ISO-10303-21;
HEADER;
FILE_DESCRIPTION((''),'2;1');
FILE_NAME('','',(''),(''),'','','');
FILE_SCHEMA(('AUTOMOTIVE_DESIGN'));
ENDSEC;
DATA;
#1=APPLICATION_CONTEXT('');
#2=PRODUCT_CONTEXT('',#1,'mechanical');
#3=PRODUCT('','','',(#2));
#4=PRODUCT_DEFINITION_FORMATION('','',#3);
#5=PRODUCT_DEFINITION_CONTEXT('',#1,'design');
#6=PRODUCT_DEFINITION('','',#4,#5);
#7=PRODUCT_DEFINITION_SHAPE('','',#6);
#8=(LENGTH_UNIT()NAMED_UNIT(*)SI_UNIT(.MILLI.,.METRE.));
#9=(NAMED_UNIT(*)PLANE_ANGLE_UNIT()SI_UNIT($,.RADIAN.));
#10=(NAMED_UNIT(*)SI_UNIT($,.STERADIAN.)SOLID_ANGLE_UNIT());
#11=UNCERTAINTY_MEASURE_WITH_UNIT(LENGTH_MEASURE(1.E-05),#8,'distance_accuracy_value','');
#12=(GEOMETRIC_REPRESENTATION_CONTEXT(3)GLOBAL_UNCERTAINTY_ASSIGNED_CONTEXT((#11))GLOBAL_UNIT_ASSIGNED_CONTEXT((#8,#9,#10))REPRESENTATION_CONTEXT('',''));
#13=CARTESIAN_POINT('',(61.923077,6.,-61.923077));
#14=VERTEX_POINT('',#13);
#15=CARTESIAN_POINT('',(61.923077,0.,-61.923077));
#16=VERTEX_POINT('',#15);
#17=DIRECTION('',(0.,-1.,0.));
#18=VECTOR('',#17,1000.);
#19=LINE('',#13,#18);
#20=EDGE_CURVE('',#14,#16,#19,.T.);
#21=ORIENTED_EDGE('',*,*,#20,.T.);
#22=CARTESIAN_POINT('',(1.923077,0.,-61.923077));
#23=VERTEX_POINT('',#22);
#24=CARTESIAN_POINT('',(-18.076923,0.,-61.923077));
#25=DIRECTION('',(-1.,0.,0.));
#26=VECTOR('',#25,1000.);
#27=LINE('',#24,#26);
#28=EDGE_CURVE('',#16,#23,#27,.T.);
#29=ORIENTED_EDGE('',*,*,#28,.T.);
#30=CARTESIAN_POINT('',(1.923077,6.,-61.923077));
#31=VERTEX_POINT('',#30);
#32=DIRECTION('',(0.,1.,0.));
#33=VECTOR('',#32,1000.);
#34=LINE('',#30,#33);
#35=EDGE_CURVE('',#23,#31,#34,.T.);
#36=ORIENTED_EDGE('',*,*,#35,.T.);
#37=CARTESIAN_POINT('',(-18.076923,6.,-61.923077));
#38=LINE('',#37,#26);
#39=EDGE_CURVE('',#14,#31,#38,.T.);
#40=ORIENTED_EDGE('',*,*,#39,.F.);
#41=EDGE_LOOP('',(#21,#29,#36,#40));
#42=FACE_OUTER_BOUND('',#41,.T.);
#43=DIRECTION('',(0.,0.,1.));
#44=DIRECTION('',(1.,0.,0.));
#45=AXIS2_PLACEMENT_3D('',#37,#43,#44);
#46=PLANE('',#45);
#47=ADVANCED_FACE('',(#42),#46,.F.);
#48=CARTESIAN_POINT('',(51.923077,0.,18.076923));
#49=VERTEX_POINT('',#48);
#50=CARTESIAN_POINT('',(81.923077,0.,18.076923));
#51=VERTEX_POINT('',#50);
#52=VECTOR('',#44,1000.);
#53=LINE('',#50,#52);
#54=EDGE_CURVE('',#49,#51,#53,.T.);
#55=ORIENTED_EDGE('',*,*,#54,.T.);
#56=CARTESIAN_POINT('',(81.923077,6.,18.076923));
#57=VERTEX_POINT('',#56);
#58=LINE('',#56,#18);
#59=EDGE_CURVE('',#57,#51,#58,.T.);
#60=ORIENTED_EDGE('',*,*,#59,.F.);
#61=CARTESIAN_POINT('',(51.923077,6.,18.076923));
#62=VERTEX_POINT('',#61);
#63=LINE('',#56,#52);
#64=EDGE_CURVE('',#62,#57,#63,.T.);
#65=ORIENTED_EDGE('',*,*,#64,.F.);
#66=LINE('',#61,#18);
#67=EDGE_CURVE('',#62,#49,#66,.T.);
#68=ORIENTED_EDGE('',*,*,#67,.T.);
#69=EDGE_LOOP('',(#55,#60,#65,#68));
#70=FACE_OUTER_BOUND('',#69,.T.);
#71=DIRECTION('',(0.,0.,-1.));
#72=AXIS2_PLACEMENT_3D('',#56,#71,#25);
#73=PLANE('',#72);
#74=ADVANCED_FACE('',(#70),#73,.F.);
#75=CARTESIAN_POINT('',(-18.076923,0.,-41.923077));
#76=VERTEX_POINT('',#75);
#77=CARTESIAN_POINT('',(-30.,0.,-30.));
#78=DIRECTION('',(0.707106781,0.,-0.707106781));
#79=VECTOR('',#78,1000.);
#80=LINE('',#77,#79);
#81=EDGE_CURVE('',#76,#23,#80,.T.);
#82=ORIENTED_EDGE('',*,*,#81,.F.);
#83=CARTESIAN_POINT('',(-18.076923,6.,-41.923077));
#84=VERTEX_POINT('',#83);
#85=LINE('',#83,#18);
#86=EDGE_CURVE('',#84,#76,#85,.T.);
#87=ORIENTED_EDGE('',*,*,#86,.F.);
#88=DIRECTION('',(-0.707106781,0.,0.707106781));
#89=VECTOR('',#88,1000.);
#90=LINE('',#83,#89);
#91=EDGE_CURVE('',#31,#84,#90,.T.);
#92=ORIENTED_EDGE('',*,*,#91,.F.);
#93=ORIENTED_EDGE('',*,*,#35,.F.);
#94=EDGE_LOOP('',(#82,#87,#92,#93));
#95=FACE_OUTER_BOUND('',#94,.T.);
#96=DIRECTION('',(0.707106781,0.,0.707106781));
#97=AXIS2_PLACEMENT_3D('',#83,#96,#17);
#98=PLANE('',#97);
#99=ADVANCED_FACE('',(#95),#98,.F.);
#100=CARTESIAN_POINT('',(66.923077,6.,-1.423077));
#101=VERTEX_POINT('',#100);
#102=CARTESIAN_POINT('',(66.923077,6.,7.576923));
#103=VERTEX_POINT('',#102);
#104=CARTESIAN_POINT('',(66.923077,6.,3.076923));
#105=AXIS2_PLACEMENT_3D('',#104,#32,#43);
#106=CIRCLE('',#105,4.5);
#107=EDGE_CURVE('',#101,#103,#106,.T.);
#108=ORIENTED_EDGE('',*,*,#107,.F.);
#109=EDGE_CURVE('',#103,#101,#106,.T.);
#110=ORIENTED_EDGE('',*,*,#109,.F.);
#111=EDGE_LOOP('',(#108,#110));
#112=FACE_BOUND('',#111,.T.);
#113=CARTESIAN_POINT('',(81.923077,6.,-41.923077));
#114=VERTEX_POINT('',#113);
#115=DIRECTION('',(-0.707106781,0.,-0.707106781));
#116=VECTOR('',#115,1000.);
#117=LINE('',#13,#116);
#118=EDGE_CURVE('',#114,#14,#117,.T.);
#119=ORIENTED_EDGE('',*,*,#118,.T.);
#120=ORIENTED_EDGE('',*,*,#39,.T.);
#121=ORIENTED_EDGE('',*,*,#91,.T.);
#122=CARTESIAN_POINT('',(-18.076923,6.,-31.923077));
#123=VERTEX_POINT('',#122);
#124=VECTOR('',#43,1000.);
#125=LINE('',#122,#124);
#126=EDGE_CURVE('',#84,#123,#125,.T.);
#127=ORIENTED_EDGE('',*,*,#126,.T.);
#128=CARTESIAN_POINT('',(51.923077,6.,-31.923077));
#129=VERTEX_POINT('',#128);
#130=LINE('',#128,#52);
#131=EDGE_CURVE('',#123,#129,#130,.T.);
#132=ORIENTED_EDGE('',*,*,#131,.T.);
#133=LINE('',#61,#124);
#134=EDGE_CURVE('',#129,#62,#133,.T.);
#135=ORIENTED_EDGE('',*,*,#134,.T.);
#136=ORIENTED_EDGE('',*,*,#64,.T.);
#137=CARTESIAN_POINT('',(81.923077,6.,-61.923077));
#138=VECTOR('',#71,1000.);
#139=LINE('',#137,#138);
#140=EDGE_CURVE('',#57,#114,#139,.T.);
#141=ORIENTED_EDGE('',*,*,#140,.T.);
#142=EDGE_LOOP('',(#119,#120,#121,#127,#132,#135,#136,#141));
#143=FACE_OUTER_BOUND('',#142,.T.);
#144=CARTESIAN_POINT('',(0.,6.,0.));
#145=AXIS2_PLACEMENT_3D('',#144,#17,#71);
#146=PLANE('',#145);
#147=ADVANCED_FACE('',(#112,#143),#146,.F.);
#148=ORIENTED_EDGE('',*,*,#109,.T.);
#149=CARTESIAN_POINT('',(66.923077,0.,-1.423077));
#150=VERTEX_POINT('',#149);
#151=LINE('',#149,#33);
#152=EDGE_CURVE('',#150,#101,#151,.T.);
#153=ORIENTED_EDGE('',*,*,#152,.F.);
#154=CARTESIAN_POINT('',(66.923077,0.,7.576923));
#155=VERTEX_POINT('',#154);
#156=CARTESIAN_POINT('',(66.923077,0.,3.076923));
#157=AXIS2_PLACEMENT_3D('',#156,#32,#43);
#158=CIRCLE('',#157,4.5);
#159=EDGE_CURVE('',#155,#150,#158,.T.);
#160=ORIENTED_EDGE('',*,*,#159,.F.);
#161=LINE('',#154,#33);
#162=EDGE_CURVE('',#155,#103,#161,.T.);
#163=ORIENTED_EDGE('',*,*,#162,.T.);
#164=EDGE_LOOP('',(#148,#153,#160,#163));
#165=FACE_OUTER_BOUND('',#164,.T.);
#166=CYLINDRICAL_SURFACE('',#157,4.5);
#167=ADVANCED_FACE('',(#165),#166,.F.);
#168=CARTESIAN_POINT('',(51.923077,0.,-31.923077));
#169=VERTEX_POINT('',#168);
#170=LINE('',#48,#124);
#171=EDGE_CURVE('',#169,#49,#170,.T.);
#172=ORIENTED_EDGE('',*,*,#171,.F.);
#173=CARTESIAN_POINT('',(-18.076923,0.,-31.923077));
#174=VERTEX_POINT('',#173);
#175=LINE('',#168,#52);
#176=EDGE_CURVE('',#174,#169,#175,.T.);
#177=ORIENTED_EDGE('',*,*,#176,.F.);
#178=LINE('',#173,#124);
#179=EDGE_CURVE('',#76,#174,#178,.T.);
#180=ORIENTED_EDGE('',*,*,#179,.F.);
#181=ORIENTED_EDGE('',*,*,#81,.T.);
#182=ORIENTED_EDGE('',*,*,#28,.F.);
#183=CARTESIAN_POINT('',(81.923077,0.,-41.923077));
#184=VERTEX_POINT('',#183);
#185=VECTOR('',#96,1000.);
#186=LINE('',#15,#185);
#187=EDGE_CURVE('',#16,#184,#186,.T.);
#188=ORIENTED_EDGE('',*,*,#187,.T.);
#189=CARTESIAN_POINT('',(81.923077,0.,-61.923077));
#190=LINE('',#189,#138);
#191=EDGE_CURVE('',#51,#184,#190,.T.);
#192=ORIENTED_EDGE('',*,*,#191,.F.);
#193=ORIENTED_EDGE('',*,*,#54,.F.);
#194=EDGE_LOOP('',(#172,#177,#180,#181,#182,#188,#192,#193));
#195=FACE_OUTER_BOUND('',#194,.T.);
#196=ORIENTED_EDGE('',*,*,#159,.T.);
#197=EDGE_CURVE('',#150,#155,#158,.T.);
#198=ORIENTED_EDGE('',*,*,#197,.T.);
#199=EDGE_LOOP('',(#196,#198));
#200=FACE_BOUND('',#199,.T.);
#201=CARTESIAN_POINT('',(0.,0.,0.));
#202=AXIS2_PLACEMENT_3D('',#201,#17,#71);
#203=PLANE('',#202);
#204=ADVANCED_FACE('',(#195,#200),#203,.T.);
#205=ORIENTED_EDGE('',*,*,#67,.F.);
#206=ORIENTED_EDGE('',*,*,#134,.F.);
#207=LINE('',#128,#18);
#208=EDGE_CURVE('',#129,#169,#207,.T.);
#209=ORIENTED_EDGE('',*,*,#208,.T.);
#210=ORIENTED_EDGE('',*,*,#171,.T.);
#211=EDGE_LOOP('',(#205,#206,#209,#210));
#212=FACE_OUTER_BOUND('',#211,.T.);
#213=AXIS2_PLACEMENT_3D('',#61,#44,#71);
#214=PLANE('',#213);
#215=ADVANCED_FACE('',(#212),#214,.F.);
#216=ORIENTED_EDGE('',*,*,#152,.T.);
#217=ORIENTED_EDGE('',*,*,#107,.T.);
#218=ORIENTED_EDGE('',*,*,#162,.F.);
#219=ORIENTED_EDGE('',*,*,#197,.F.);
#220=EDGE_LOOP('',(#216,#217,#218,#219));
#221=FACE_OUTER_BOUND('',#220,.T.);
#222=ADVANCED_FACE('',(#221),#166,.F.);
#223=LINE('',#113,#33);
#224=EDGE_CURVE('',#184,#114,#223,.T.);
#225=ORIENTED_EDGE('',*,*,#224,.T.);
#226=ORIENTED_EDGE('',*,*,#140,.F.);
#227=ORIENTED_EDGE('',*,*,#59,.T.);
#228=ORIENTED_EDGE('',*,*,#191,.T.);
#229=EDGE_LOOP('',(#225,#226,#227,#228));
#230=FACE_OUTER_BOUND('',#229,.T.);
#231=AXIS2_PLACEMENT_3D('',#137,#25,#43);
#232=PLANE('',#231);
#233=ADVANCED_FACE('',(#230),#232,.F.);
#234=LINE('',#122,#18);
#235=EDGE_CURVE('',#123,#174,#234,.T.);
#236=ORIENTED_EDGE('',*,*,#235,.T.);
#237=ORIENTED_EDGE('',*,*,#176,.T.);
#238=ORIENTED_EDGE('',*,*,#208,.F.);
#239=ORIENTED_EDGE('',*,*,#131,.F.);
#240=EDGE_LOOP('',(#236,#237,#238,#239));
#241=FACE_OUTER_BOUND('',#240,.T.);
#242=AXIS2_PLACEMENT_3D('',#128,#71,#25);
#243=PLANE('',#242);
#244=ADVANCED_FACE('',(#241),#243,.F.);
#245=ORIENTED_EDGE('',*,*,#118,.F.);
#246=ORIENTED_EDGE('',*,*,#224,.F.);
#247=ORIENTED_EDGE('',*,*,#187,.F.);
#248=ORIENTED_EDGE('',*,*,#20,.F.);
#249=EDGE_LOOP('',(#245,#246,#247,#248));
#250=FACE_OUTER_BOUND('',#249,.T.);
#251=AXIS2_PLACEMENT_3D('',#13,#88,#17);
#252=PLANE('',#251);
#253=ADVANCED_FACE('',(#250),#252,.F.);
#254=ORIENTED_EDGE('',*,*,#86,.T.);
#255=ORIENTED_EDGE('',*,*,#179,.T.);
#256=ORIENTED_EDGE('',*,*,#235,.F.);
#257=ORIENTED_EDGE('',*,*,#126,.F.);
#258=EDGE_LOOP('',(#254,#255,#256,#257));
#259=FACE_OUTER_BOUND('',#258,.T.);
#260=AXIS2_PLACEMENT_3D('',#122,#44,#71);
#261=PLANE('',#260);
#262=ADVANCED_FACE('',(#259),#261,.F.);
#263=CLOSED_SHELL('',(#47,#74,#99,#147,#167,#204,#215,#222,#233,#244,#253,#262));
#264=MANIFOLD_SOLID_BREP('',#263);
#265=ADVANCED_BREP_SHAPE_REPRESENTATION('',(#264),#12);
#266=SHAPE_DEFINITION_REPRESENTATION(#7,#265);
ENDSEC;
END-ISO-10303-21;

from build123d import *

# Parameters (mm, degrees)
BOSS_EXTRUDE1_DEPTH = 6
SKETCH2_R           = 4.5
CUT_EXTRUDE1_DEPTH  = 6
CHAMFER1_SIZE       = 20
CHAMFER2_SIZE       = 20


with BuildPart() as part:
    # Sketch1 → Boss-Extrude1 (new body)
    with BuildSketch(Plane(origin=(0, 0, 0), x_dir=(1, 0, 0), z_dir=(0, 1, 0))):
        Polygon((-18.076923077, 61.923076923), (81.923076923, 61.923076923), (81.923076923, -18.076923077), (51.923076923, -18.076923077), (51.923076923, 31.923076923), (-18.076923077, 31.923076923), align=None)
    extrude(amount=BOSS_EXTRUDE1_DEPTH)

    # Sketch2 → Cut-Extrude1 (cut)
    with BuildSketch(Plane(origin=(0, 6, 0), x_dir=(1, 0, 0), z_dir=(0, 1, 0))):
        with Locations(Location((66.923076923, -3.076923077, 0), (0, 0, 270))):
            Circle(SKETCH2_R)
    extrude(amount=-CUT_EXTRUDE1_DEPTH, mode=Mode.SUBTRACT)

    # Chamfer1
    chamfer1_edges = [part.edges().sort_by_distance(p)[0] for p in [
        (-18.076923077, 3, -61.923076923),
    ]]
    chamfer(chamfer1_edges, length=CHAMFER1_SIZE)

    # Chamfer2
    chamfer2_edges = [part.edges().sort_by_distance(p)[0] for p in [
        (81.923076923, 3, -61.923076923),
    ]]
    chamfer(chamfer2_edges, length=CHAMFER2_SIZE)


solid = part.part
